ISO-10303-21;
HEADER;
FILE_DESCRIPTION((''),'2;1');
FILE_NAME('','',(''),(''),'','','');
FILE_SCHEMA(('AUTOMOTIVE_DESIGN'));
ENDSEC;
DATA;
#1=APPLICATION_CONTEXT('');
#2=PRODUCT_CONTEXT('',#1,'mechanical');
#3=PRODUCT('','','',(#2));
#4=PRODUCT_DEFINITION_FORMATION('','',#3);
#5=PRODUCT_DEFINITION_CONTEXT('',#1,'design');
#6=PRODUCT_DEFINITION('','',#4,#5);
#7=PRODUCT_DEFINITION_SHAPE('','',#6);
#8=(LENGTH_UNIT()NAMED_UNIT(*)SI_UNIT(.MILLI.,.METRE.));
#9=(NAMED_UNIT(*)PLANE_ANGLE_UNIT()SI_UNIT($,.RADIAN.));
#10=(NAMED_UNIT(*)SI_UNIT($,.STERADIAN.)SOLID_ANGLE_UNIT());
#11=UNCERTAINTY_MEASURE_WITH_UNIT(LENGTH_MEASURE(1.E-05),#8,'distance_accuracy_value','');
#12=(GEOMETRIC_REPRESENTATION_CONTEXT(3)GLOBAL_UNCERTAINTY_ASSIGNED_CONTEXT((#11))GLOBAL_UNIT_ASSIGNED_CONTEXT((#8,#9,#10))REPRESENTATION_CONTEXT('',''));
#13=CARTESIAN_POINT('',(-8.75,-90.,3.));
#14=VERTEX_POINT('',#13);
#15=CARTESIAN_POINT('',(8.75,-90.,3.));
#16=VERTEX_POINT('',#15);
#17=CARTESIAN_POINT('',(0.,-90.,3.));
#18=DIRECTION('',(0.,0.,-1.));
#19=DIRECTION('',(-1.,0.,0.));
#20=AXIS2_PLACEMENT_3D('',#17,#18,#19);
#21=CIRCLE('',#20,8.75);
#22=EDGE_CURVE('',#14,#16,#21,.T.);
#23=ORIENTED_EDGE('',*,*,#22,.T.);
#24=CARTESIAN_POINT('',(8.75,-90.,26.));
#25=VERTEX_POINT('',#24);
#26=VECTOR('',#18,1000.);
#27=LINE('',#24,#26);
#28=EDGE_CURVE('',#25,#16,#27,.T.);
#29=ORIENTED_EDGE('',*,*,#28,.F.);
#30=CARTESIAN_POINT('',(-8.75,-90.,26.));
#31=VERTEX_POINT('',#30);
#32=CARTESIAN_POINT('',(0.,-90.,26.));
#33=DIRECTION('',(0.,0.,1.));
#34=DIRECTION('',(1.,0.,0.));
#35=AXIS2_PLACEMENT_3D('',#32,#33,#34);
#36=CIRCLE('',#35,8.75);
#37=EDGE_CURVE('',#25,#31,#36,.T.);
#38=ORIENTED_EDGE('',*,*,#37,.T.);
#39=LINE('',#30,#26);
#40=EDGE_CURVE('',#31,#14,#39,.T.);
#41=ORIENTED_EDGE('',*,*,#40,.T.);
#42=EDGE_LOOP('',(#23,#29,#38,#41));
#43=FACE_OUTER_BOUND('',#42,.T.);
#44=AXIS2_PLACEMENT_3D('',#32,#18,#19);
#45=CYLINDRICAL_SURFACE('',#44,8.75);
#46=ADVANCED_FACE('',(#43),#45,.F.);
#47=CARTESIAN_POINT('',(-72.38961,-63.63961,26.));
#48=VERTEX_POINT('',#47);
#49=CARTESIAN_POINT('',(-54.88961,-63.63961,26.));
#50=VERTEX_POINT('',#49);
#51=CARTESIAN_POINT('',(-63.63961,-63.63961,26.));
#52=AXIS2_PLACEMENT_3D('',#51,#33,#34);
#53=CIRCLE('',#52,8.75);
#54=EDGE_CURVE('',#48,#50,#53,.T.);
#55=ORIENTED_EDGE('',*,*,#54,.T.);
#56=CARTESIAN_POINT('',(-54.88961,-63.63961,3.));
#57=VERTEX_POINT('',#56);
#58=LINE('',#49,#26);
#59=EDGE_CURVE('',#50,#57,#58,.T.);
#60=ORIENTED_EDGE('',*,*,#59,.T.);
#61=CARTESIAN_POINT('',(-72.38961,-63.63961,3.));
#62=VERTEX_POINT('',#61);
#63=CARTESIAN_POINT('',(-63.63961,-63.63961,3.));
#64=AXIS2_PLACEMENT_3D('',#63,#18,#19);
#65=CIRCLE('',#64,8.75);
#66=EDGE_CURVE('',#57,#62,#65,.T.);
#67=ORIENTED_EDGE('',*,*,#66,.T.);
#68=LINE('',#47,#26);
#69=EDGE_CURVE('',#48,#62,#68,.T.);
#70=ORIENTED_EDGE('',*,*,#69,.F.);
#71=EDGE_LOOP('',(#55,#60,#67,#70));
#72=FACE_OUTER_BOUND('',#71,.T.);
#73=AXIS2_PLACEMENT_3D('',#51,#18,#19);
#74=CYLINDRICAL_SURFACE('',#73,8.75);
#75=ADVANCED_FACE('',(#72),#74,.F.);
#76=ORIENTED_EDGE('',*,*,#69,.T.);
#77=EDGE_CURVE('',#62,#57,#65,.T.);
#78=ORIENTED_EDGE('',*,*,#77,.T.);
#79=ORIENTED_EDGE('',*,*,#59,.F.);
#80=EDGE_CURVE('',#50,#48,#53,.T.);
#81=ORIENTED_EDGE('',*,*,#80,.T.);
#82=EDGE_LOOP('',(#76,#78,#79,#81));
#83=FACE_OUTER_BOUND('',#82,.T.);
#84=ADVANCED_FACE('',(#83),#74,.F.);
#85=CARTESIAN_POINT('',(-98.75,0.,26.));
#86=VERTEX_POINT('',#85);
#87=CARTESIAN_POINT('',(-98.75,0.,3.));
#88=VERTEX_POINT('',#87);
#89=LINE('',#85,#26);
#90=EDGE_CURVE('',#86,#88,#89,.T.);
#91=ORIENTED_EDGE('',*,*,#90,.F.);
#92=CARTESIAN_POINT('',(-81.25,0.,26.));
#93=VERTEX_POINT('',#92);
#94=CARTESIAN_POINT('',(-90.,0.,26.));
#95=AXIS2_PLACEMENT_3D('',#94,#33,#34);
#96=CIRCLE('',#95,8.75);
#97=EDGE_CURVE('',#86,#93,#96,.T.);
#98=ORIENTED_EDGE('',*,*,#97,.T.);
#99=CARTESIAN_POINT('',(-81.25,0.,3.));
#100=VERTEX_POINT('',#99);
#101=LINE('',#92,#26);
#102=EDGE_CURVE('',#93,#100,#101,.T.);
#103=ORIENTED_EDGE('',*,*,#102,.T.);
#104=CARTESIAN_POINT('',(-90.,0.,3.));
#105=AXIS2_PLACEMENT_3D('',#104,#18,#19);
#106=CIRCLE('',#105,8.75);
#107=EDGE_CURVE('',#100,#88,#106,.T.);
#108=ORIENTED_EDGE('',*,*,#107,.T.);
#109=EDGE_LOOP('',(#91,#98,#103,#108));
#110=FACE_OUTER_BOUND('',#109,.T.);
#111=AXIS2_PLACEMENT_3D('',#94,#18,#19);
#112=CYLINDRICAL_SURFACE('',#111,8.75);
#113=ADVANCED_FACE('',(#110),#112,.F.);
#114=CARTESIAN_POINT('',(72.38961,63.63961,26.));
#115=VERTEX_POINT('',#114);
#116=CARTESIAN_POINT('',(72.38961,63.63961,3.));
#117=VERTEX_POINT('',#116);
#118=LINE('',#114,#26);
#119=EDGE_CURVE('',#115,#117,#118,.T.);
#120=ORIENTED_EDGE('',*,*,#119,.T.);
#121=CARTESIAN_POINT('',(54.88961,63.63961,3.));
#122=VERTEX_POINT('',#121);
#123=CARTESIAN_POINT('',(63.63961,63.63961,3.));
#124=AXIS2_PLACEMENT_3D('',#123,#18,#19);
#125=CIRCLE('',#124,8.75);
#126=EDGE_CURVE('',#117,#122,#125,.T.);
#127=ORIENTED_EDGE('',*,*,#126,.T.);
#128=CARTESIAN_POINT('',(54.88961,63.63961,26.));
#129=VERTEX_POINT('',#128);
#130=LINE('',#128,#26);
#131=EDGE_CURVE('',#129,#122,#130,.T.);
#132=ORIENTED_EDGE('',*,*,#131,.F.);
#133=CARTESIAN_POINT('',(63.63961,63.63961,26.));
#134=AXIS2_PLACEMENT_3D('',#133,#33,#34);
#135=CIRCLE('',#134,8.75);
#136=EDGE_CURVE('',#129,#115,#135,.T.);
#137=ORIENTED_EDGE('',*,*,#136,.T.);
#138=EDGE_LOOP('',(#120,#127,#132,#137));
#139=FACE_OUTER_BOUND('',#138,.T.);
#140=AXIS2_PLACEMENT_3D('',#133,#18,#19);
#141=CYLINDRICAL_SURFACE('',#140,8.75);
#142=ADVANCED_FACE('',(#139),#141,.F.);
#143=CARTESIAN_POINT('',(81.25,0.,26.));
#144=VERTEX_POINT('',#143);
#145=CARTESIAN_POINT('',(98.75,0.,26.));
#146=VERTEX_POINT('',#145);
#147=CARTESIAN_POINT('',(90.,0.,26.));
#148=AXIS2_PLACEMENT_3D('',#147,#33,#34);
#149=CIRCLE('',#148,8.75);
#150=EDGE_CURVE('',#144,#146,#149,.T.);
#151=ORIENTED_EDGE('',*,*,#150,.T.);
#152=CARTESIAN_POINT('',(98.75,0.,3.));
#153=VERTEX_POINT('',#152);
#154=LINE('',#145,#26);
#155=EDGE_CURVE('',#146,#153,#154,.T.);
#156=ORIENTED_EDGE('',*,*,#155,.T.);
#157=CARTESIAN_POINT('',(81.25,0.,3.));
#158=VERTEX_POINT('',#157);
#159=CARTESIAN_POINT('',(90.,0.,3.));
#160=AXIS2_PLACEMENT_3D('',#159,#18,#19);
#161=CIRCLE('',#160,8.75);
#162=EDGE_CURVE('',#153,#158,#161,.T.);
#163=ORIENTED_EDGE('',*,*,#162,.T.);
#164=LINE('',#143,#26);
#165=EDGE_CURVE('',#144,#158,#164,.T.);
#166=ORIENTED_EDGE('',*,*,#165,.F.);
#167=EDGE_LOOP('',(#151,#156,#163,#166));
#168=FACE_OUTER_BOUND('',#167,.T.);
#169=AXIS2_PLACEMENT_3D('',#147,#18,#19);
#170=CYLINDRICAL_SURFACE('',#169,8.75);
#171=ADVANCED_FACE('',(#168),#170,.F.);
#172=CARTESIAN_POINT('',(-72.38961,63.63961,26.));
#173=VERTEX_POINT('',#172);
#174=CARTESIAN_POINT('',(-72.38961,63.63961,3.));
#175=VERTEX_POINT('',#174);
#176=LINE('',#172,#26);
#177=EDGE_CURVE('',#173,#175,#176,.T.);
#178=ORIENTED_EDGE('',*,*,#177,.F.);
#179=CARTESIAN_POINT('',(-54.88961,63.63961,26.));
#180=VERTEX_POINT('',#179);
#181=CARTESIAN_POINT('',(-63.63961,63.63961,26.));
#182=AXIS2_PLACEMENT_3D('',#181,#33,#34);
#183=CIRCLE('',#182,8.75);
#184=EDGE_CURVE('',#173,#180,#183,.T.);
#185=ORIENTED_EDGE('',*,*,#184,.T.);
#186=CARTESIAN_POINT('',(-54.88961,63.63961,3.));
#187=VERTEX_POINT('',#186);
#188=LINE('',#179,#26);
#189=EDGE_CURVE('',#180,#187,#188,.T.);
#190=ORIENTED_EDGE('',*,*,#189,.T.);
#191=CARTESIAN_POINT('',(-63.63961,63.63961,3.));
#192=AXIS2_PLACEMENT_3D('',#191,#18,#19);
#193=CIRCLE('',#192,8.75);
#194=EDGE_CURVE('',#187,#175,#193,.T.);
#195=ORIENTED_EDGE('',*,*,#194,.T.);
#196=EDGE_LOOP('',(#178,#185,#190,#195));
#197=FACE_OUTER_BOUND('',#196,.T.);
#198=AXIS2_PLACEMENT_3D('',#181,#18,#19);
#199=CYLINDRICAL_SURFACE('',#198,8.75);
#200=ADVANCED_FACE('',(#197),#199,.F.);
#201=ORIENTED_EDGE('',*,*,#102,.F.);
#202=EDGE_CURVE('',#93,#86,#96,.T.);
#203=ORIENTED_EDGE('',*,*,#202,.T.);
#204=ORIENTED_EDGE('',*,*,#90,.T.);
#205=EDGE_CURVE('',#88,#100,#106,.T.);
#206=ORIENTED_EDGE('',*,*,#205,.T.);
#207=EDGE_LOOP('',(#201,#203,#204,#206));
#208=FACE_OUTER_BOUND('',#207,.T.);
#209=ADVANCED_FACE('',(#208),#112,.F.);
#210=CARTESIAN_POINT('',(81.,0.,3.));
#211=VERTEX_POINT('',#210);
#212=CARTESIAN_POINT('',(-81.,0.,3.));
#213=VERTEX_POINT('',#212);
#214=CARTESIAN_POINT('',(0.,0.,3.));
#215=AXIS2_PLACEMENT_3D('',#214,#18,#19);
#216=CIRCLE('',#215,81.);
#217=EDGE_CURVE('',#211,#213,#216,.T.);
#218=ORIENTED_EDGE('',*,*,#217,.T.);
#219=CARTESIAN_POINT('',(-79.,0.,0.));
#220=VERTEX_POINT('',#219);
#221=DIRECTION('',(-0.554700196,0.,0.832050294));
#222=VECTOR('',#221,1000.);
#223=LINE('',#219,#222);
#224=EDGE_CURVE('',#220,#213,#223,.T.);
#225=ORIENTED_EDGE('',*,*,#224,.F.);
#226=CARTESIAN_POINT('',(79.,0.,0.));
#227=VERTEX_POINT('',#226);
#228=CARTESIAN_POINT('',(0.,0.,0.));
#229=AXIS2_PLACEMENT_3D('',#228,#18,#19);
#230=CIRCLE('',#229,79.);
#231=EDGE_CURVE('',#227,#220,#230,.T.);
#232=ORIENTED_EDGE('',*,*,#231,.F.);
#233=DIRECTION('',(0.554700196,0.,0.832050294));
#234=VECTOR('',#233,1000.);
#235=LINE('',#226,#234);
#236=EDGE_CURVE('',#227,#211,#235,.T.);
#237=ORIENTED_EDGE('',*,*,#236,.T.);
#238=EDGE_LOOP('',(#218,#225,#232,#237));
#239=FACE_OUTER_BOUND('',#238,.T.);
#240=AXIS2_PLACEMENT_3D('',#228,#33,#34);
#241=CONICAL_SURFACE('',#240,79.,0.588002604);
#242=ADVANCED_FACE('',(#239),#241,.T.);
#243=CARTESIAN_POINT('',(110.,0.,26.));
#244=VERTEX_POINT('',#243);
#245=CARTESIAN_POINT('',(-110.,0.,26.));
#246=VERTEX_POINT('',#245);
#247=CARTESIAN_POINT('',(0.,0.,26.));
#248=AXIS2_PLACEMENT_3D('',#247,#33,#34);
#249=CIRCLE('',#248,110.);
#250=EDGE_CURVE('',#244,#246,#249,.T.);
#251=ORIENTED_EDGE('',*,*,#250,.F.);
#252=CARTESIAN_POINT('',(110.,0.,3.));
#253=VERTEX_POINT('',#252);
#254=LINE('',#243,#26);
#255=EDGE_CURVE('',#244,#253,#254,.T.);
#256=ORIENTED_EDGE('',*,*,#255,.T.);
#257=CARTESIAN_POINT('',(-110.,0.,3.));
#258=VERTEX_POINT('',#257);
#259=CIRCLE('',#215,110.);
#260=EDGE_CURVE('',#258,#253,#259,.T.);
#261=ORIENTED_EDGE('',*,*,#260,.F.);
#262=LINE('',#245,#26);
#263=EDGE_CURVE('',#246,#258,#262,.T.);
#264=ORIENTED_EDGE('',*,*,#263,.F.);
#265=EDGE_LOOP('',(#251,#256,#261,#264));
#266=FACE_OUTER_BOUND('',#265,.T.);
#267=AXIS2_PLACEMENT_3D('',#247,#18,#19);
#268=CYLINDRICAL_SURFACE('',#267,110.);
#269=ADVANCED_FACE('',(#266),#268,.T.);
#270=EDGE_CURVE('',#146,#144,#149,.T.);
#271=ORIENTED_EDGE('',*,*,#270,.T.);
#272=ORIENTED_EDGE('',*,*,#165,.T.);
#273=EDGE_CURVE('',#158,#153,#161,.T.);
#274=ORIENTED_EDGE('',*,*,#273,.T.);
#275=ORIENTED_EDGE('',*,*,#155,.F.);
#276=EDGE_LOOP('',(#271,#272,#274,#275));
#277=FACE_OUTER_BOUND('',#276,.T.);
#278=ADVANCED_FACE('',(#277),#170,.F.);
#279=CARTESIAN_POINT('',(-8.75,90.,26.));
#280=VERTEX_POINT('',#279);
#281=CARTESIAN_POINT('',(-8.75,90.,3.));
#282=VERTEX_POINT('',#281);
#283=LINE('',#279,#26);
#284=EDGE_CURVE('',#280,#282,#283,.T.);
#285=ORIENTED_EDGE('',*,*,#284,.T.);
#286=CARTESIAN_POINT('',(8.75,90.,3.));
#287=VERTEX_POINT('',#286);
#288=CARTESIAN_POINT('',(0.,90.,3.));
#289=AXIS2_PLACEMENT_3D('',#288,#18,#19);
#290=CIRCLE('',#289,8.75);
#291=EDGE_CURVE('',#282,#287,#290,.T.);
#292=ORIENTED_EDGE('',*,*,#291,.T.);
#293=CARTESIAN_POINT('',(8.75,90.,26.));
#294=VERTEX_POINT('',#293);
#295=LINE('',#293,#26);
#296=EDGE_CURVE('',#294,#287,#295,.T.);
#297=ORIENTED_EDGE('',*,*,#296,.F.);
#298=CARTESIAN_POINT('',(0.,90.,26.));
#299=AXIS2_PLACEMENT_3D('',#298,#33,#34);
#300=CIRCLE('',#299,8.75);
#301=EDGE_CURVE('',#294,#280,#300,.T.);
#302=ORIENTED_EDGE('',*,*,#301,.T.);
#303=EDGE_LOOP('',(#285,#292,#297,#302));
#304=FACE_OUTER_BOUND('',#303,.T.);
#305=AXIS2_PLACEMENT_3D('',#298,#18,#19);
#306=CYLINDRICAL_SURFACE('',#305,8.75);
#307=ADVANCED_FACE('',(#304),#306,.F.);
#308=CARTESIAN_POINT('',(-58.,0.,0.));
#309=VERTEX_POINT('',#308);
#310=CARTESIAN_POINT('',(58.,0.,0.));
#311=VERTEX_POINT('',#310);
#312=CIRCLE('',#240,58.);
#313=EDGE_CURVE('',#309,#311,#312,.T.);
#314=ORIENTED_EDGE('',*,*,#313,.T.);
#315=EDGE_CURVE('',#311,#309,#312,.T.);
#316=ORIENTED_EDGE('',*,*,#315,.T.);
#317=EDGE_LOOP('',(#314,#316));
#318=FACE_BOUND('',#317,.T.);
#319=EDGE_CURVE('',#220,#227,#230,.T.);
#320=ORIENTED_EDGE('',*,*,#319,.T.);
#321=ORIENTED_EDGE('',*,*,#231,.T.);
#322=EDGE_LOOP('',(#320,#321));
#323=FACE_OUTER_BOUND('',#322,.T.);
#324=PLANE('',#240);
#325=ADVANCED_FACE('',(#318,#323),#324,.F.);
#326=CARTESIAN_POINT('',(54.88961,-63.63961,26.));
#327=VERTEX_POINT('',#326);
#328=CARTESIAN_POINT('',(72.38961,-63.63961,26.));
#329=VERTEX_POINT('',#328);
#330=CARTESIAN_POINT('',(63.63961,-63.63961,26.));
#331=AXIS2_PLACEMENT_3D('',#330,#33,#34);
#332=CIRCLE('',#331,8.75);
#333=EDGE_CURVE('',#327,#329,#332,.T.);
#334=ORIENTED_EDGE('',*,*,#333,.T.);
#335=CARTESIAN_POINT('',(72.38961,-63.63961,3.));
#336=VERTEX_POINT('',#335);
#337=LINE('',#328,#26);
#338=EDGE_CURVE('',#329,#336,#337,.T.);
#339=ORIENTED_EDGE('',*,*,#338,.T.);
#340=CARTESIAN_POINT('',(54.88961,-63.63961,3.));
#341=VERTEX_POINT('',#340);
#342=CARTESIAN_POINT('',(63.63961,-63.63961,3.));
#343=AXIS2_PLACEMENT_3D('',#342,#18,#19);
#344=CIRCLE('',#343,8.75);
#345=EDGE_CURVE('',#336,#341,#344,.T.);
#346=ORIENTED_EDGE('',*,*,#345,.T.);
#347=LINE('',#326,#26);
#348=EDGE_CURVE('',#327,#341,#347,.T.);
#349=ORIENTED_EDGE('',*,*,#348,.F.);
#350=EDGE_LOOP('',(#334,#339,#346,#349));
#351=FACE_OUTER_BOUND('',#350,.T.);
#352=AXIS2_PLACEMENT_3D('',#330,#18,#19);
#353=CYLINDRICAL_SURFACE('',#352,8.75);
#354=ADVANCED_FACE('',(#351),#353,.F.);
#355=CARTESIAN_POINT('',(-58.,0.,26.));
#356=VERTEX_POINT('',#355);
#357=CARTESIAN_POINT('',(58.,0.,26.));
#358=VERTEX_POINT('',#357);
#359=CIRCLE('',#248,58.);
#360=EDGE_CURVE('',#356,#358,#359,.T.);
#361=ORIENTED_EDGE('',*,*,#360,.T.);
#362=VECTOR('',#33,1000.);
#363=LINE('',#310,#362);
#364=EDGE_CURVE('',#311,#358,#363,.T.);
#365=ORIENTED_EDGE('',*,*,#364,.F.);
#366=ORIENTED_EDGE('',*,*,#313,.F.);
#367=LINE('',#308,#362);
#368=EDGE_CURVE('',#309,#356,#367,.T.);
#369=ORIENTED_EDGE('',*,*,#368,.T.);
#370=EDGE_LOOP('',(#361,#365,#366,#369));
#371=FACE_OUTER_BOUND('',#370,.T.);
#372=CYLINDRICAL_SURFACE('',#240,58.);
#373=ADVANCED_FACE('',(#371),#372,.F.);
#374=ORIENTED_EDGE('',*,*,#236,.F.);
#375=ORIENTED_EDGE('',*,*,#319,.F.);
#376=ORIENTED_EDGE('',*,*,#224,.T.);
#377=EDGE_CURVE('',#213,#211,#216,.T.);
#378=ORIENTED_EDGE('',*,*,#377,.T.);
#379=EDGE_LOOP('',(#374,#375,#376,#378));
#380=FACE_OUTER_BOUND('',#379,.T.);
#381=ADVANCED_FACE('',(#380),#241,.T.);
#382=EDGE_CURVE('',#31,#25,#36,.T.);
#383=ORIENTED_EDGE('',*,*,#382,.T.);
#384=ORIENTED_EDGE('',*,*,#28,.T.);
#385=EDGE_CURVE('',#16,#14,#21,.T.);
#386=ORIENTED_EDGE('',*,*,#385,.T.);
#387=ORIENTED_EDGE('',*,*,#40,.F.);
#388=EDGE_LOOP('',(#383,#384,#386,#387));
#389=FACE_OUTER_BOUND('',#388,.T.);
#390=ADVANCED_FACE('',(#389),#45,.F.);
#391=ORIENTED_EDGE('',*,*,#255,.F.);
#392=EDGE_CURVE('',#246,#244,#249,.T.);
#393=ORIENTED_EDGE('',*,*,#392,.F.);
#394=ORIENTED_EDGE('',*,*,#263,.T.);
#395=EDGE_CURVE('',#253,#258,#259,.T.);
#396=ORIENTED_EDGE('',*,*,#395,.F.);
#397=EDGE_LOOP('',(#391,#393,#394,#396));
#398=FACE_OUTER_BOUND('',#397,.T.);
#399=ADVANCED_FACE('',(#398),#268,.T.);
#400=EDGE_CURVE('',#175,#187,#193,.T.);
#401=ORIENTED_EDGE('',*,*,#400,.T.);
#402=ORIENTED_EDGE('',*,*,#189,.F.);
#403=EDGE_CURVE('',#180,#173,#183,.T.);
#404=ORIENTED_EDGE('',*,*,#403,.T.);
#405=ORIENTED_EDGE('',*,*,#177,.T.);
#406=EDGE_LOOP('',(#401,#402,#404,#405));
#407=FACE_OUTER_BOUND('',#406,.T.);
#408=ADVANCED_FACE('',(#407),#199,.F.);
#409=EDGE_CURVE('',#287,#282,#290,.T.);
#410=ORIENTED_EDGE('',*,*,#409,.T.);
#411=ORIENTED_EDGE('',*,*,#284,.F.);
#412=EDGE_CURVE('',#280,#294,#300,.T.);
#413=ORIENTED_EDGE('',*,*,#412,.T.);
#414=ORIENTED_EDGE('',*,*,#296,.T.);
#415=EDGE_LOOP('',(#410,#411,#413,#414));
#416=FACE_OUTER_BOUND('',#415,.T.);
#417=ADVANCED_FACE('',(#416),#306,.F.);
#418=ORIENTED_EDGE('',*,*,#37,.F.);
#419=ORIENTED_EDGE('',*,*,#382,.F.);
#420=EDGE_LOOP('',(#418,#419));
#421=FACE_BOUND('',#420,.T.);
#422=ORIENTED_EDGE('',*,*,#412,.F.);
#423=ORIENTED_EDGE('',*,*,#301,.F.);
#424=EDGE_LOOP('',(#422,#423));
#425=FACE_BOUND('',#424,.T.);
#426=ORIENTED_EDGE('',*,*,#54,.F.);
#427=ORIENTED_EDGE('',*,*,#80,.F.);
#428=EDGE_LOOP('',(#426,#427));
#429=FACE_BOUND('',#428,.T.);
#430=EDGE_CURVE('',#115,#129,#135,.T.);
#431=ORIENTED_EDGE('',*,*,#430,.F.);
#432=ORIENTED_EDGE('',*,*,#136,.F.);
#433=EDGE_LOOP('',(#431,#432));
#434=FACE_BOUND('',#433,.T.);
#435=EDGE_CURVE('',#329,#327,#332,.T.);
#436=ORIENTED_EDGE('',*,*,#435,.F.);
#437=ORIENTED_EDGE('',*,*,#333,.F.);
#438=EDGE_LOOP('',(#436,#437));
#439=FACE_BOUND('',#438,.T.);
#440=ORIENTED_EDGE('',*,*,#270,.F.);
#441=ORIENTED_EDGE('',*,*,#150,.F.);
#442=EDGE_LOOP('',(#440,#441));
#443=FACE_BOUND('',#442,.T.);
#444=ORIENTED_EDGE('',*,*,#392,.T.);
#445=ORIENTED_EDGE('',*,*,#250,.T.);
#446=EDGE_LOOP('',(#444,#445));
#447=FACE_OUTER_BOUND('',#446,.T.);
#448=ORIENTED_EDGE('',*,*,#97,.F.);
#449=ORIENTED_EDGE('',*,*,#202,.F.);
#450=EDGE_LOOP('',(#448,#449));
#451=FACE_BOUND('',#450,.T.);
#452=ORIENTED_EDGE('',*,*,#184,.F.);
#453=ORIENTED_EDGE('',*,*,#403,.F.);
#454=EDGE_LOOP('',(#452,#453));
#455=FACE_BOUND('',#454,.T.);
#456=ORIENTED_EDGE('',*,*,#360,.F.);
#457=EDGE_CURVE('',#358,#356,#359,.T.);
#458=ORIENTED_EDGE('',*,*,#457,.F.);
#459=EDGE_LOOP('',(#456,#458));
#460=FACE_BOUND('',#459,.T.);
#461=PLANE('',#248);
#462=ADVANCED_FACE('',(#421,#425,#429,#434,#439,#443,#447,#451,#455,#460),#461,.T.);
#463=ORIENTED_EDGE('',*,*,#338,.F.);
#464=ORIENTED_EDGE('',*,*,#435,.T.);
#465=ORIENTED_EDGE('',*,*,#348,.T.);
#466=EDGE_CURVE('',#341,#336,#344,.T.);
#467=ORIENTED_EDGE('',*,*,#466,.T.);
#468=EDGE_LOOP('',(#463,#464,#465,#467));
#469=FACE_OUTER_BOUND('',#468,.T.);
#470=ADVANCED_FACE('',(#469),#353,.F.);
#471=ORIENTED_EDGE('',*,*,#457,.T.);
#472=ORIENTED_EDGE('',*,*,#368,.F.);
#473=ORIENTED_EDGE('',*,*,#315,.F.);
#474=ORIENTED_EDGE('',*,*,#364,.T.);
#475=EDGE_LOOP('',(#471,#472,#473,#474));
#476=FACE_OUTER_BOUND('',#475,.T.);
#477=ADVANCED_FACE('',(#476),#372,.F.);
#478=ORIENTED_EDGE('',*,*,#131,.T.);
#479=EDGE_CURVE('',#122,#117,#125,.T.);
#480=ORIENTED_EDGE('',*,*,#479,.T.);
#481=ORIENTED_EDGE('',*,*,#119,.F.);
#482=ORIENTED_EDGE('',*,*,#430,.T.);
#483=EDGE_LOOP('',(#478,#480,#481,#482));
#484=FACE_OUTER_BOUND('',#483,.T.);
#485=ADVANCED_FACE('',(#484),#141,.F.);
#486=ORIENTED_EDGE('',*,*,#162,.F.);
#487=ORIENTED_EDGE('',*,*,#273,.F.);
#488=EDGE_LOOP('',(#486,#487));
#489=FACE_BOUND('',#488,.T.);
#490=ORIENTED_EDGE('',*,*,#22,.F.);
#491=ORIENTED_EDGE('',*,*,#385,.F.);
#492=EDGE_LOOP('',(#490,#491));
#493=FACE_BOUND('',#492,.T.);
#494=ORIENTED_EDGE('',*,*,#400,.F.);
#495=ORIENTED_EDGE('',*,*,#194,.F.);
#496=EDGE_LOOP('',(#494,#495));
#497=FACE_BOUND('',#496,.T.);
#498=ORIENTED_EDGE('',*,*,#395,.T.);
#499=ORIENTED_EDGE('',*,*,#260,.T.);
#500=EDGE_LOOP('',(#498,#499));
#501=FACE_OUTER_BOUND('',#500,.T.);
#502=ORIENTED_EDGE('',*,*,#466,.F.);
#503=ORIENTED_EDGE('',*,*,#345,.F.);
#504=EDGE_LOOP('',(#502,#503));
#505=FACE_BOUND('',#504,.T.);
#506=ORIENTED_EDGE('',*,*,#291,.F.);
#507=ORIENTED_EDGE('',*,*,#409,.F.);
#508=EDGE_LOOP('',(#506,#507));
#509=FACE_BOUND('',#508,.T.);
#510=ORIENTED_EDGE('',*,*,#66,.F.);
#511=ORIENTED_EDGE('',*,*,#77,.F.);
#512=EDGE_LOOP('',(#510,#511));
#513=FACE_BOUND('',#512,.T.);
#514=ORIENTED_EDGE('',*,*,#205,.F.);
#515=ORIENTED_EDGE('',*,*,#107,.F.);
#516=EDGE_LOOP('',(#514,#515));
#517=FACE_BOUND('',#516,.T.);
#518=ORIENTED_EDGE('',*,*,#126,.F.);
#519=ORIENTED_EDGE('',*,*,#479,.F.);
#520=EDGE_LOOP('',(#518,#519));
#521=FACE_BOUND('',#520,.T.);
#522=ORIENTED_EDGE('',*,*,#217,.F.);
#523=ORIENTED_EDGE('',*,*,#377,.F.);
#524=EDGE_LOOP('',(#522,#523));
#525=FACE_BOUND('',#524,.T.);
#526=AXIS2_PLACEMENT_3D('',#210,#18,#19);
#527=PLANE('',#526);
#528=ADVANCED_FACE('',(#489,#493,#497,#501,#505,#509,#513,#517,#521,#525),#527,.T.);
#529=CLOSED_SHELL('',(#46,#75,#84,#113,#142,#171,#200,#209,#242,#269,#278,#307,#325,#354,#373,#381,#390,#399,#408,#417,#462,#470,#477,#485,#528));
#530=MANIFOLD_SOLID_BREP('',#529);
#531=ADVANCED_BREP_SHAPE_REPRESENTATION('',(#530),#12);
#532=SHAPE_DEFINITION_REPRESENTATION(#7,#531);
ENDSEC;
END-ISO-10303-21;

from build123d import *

# Parameters (mm, degrees)
SKETCH1_R               = 110
SKETCH1_R_2             = 8.75
BOSS_EXTRUDE1_DEPTH     = 26
CUT_EXTRUDE2_DEPTH      = 158.721273137
CUT_EXTRUDE2_DEPTH_BACK = 158.721273137
SKETCH3_R               = 58


with BuildPart() as part:
    # Sketch1 → Boss-Extrude1 (new body)
    with BuildSketch(Plane.XY):
        with Locations(Location((0, 0, 0), (0, 0, 180))):
            Circle(SKETCH1_R)
        with Locations(Location((0, 90, 0), (0, 0, 180))):
            Circle(SKETCH1_R_2, mode=Mode.SUBTRACT)
        with Locations(Location((63.639610307, 63.639610307, 0), (0, 0, 180))):
            Circle(SKETCH1_R_2, mode=Mode.SUBTRACT)
        with Locations(Location((90, 0, 0), (0, 0, 180))):
            Circle(SKETCH1_R_2, mode=Mode.SUBTRACT)
        with Locations(Location((63.639610307, -63.639610307, 0), (0, 0, 180))):
            Circle(SKETCH1_R_2, mode=Mode.SUBTRACT)
        with Locations(Location((0, -90, 0), (0, 0, 180))):
            Circle(SKETCH1_R_2, mode=Mode.SUBTRACT)
        with Locations(Location((-63.639610307, -63.639610307, 0), (0, 0, 180))):
            Circle(SKETCH1_R_2, mode=Mode.SUBTRACT)
        with Locations(Location((-90, 0, 0), (0, 0, 180))):
            Circle(SKETCH1_R_2, mode=Mode.SUBTRACT)
        with Locations(Location((-63.639610307, 63.639610307, 0), (0, 0, 180))):
            Circle(SKETCH1_R_2, mode=Mode.SUBTRACT)
    extrude(amount=BOSS_EXTRUDE1_DEPTH)

    # Sketch3 → Cut-Extrude2 (cut, two sides: drawn at the far end of the back side and taken through both)
    with BuildSketch(Plane.XY.offset(26).offset(-CUT_EXTRUDE2_DEPTH_BACK)):
        Circle(SKETCH3_R)
    extrude(amount=CUT_EXTRUDE2_DEPTH + CUT_EXTRUDE2_DEPTH_BACK, mode=Mode.SUBTRACT)

    # Sketch4 → Cut-Revolve1 (revolve, cut)
    with BuildSketch(Plane(origin=(0, 0, 0), x_dir=(1, 0, 0), z_dir=(0, 1, 0)), mode=Mode.PRIVATE) as cut_revolve1_sk:
        Polygon((79, 0), (81, -3), (110, -3), (110, 0), align=None)
    revolve(cut_revolve1_sk.sketch.rotate(Axis((0, 0, 0), (0, 0, 1)), 180), axis=Axis((0, 0, 0), (0, 0, 1)), mode=Mode.SUBTRACT)


solid = part.part
